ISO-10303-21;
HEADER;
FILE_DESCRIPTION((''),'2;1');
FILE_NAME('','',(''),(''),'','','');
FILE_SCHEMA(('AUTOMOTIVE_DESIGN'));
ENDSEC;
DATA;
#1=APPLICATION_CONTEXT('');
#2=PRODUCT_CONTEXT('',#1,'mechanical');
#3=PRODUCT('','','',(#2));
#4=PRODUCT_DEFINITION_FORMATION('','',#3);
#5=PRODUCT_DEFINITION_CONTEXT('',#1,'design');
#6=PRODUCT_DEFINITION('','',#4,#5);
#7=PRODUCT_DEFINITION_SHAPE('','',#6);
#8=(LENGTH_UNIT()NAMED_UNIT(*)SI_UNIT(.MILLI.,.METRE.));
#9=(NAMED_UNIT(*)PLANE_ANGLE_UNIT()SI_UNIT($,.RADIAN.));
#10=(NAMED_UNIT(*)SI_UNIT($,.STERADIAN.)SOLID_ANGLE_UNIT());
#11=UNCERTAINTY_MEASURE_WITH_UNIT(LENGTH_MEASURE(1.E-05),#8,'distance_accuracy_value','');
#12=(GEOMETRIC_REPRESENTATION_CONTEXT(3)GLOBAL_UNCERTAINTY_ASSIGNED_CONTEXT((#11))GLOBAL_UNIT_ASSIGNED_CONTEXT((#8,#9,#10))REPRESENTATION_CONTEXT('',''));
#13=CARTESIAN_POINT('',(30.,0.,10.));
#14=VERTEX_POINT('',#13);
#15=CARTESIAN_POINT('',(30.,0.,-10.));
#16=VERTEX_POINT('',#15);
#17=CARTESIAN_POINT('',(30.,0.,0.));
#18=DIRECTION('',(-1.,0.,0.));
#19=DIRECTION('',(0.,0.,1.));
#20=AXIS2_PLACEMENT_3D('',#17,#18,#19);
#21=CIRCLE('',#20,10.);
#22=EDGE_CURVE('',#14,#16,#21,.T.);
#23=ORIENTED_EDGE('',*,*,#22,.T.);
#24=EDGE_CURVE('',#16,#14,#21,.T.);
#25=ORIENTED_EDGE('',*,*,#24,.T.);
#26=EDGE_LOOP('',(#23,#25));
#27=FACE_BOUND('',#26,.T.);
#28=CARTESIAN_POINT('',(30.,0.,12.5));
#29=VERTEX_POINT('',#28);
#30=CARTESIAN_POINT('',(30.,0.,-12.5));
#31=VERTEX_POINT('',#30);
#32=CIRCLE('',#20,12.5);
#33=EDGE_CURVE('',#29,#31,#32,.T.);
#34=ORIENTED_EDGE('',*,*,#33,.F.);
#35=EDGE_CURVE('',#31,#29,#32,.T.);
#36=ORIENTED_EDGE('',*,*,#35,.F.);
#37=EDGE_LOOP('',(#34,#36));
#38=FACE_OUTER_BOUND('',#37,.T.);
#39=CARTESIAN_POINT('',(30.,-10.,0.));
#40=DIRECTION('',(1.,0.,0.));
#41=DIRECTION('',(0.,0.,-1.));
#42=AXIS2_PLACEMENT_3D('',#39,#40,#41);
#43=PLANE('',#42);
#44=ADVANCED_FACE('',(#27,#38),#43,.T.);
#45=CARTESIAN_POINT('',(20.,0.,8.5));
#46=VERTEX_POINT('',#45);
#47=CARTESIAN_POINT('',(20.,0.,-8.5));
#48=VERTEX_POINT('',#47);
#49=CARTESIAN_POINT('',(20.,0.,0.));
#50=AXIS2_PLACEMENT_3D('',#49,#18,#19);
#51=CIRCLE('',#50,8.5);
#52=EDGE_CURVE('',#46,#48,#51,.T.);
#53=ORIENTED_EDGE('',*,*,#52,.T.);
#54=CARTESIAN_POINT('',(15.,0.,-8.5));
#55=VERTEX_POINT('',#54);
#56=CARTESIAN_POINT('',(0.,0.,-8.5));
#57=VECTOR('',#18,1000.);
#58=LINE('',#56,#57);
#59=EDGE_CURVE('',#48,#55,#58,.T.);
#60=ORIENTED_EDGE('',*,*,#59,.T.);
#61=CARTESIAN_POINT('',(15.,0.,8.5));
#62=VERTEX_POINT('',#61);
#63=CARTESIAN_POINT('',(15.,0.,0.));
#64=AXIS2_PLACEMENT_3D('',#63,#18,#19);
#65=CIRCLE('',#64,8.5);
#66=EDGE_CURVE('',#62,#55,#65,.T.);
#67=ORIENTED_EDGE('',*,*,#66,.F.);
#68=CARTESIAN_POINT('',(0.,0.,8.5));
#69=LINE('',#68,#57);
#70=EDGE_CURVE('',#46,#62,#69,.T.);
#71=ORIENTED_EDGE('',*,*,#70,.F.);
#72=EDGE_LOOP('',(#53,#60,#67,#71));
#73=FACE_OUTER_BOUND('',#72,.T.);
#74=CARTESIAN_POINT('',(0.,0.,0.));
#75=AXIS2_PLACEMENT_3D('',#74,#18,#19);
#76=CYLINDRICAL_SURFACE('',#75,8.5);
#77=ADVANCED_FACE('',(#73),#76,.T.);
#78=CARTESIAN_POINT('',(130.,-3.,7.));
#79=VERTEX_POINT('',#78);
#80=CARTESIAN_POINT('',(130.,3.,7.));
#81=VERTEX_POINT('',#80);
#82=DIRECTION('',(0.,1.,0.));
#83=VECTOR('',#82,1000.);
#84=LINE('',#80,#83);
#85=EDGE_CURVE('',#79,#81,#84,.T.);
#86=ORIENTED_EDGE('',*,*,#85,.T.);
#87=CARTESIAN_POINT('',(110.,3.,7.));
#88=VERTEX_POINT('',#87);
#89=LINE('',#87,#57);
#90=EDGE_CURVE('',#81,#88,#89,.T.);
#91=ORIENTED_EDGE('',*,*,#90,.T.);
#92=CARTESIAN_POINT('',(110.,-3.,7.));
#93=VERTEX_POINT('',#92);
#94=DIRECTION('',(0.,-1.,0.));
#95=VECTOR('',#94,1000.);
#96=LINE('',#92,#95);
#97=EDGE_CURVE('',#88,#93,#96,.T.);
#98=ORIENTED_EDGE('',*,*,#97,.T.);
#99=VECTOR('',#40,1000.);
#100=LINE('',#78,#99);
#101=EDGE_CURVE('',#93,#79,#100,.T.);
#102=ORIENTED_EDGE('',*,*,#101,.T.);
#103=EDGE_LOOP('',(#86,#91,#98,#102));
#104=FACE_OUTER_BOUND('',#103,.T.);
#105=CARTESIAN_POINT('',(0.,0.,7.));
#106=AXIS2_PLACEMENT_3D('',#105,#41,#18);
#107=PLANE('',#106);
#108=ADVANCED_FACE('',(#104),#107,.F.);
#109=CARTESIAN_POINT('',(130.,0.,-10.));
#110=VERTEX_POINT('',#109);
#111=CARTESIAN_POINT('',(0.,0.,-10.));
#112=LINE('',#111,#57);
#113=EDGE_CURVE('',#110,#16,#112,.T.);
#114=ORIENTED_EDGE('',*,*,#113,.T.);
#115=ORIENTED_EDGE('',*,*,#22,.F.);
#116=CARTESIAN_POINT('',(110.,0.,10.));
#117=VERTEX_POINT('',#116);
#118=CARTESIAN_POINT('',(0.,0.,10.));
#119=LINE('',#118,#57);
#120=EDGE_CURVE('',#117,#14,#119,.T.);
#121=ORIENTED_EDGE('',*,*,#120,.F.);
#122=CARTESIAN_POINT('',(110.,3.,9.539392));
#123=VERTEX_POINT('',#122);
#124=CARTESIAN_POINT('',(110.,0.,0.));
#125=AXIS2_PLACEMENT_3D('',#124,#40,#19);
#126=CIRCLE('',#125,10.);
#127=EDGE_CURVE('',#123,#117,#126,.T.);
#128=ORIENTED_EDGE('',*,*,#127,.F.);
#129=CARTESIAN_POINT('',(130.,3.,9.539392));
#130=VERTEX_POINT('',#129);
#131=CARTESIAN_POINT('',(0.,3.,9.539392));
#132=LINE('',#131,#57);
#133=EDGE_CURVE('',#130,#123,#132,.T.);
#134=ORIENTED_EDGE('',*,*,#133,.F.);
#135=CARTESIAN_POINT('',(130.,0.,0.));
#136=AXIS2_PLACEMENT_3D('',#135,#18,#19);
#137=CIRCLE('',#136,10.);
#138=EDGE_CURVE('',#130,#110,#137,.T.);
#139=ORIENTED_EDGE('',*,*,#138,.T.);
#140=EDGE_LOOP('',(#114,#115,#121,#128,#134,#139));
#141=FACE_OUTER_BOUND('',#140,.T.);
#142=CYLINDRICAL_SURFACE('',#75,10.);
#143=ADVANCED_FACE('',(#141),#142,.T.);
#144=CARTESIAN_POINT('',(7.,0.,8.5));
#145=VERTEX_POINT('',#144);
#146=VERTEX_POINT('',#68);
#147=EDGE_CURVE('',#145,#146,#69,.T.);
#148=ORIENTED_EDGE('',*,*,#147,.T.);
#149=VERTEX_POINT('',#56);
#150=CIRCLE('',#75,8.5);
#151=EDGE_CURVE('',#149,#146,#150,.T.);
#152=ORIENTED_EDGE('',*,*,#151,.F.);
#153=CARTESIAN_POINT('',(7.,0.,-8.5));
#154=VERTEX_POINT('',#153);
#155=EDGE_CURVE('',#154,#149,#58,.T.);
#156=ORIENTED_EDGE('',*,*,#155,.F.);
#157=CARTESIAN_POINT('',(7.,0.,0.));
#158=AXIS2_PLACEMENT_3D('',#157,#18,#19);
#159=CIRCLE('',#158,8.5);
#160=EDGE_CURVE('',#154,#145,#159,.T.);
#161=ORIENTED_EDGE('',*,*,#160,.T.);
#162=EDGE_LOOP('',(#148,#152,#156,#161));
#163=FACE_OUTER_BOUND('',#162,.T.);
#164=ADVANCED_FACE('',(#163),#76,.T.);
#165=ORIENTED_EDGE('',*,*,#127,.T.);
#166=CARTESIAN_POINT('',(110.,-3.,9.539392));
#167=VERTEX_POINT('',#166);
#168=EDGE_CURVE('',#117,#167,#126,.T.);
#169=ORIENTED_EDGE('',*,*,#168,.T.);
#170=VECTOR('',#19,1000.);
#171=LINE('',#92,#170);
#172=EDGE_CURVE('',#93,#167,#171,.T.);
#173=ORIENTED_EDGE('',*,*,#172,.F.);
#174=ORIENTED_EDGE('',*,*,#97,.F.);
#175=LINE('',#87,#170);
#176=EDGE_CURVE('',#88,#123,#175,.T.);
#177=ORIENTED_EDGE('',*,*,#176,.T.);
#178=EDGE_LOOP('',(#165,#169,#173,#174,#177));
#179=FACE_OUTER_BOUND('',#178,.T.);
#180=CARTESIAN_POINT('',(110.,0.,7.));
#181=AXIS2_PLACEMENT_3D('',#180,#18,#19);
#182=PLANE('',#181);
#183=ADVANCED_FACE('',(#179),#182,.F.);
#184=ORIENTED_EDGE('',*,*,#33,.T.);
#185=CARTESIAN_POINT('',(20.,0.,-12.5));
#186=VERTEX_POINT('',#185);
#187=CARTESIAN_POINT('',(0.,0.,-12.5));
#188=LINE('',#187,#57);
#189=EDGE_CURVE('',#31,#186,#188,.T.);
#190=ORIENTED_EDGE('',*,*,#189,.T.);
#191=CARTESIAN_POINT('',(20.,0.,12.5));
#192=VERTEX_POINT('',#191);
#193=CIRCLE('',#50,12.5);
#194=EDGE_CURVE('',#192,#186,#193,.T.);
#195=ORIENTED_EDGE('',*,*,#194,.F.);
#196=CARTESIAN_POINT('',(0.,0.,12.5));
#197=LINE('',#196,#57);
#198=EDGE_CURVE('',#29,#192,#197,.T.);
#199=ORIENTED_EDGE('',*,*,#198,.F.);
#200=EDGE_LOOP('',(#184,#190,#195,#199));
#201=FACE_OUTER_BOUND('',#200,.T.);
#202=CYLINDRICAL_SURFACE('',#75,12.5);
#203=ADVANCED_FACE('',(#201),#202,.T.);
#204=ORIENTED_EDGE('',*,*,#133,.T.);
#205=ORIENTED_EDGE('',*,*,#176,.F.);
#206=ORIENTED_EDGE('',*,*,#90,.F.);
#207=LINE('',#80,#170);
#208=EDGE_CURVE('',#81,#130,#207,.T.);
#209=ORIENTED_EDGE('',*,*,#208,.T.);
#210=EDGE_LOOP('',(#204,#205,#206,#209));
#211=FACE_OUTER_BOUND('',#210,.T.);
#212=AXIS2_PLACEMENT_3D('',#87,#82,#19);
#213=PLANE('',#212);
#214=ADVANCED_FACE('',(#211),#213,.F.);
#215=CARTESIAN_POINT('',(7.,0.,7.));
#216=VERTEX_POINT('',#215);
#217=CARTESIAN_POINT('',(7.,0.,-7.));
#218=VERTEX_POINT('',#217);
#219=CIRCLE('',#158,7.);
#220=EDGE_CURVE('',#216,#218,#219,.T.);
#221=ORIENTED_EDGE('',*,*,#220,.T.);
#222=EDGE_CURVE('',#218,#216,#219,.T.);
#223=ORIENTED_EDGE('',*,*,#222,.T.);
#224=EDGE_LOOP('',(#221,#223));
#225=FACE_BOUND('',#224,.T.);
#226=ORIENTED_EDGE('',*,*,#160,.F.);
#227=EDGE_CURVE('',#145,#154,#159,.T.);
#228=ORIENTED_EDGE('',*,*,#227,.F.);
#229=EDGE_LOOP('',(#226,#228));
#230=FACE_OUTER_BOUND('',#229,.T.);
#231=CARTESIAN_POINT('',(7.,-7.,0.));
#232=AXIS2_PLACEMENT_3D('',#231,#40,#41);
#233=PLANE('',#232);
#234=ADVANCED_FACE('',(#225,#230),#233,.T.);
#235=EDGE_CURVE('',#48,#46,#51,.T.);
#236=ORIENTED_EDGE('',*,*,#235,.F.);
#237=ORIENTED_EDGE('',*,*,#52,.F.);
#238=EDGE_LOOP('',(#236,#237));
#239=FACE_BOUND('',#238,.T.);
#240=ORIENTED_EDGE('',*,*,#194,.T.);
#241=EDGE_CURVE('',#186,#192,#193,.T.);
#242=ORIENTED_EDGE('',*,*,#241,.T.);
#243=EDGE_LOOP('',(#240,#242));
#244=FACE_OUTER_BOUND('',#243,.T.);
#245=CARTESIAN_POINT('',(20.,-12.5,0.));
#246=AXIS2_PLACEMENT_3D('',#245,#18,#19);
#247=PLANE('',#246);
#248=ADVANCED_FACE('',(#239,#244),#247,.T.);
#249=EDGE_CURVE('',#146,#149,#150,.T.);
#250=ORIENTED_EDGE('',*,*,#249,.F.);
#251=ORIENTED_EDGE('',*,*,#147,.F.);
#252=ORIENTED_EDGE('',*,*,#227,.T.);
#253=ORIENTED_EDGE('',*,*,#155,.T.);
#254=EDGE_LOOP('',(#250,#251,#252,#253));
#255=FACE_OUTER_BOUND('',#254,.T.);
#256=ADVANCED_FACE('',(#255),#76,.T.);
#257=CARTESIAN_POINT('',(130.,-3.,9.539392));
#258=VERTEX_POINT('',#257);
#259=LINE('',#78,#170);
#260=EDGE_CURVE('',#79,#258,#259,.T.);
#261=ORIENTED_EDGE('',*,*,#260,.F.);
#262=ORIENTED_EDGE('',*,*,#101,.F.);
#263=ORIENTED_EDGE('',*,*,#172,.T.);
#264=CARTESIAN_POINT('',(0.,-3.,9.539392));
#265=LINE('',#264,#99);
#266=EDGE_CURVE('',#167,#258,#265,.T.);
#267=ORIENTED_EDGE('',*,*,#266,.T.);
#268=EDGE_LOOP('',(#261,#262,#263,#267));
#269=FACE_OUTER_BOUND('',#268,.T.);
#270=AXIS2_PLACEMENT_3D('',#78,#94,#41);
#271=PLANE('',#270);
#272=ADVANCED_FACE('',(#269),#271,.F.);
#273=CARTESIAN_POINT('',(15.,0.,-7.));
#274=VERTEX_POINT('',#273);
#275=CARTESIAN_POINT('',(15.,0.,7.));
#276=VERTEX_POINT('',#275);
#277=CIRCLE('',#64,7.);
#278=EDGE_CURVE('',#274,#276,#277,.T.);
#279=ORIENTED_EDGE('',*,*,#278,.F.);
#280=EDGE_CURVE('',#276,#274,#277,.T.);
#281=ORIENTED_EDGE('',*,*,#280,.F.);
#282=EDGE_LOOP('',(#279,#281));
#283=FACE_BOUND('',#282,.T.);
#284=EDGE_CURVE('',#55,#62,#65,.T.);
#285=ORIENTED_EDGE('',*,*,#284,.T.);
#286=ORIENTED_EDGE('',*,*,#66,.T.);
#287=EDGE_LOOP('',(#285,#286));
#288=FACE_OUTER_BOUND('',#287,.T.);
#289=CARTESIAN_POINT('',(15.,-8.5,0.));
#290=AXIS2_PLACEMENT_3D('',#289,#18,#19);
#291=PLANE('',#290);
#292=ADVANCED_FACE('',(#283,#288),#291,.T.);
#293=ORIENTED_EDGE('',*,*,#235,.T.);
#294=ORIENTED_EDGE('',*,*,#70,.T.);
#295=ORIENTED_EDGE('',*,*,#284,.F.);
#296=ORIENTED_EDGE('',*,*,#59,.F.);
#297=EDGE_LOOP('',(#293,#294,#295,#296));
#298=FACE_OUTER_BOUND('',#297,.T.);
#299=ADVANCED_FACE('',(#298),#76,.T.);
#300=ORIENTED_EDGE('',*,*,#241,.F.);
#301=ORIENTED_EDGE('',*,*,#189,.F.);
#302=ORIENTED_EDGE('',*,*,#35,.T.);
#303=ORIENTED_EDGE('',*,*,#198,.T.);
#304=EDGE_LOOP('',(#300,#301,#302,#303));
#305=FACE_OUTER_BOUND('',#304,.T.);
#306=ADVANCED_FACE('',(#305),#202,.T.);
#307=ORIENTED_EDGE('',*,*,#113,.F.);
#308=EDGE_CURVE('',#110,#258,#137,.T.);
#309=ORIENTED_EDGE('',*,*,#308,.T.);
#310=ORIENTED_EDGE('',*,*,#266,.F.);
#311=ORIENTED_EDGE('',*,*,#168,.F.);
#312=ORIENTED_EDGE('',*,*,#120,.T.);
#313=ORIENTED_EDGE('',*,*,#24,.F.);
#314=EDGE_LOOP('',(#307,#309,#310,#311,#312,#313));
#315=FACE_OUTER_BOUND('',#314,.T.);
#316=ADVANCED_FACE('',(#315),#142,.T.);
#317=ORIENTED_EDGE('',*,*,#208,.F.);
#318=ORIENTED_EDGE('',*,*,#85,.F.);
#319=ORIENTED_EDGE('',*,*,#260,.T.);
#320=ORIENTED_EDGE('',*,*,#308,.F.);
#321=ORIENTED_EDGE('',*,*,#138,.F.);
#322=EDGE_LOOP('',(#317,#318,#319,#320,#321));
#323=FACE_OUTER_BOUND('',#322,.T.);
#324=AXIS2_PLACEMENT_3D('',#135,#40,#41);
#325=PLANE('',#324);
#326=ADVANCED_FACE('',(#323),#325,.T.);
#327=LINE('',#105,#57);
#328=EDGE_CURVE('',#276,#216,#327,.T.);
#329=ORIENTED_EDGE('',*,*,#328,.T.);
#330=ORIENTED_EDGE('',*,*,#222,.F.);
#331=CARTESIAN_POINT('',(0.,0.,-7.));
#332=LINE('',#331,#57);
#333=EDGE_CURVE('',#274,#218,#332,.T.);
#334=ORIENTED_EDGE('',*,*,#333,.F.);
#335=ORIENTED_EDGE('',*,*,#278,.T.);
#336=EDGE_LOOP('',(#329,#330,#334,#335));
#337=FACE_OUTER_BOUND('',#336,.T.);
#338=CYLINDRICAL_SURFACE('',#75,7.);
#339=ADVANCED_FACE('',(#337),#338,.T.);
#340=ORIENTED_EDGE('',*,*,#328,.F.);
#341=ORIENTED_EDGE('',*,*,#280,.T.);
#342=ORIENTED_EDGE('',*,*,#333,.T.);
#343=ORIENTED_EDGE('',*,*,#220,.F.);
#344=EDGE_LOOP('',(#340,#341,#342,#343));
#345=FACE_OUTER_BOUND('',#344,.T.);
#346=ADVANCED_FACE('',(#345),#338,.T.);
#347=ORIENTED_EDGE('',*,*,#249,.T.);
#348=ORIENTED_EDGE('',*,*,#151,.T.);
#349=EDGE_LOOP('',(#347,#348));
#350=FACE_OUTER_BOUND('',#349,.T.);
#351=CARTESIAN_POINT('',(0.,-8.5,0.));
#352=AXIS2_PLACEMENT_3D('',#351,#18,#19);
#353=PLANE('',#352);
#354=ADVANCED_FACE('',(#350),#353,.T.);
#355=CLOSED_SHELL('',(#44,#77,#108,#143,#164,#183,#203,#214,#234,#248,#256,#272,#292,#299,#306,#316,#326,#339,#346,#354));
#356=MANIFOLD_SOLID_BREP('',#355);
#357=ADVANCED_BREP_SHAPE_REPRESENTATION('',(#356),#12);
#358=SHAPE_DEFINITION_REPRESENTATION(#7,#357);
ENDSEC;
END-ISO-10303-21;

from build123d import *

# Parameters (mm, degrees)
KEYWAY_6X20_DEPTH_3_DEPTH = 3


with BuildPart() as part:
    # Shaft Profile Sketch → Stepped Shaft Body (revolve)
    with BuildSketch(Plane.XY, mode=Mode.PRIVATE) as stepped_shaft_body_sk:
        Polygon((0, 0), (130, 0), (130, -10), (30, -10), (30, -12.5), (20, -12.5), (20, -8.5), (15, -8.5), (15, -7), (7, -7), (7, -8.5), (0, -8.5), align=None)
    revolve(stepped_shaft_body_sk.sketch.rotate(Axis((0, 0, 0), (1, 0, 0)), 270), axis=Axis((0, 0, 0), (1, 0, 0)))

    # Keyway Sketch → Keyway 6x20 Depth 3 (cut)
    with BuildSketch(Plane.XY.offset(10)):
        Polygon((110, 0), (110, 3), (130, 3), (130, -3), (110, -3), align=None)
    extrude(amount=-KEYWAY_6X20_DEPTH_3_DEPTH, mode=Mode.SUBTRACT)


solid = part.part
